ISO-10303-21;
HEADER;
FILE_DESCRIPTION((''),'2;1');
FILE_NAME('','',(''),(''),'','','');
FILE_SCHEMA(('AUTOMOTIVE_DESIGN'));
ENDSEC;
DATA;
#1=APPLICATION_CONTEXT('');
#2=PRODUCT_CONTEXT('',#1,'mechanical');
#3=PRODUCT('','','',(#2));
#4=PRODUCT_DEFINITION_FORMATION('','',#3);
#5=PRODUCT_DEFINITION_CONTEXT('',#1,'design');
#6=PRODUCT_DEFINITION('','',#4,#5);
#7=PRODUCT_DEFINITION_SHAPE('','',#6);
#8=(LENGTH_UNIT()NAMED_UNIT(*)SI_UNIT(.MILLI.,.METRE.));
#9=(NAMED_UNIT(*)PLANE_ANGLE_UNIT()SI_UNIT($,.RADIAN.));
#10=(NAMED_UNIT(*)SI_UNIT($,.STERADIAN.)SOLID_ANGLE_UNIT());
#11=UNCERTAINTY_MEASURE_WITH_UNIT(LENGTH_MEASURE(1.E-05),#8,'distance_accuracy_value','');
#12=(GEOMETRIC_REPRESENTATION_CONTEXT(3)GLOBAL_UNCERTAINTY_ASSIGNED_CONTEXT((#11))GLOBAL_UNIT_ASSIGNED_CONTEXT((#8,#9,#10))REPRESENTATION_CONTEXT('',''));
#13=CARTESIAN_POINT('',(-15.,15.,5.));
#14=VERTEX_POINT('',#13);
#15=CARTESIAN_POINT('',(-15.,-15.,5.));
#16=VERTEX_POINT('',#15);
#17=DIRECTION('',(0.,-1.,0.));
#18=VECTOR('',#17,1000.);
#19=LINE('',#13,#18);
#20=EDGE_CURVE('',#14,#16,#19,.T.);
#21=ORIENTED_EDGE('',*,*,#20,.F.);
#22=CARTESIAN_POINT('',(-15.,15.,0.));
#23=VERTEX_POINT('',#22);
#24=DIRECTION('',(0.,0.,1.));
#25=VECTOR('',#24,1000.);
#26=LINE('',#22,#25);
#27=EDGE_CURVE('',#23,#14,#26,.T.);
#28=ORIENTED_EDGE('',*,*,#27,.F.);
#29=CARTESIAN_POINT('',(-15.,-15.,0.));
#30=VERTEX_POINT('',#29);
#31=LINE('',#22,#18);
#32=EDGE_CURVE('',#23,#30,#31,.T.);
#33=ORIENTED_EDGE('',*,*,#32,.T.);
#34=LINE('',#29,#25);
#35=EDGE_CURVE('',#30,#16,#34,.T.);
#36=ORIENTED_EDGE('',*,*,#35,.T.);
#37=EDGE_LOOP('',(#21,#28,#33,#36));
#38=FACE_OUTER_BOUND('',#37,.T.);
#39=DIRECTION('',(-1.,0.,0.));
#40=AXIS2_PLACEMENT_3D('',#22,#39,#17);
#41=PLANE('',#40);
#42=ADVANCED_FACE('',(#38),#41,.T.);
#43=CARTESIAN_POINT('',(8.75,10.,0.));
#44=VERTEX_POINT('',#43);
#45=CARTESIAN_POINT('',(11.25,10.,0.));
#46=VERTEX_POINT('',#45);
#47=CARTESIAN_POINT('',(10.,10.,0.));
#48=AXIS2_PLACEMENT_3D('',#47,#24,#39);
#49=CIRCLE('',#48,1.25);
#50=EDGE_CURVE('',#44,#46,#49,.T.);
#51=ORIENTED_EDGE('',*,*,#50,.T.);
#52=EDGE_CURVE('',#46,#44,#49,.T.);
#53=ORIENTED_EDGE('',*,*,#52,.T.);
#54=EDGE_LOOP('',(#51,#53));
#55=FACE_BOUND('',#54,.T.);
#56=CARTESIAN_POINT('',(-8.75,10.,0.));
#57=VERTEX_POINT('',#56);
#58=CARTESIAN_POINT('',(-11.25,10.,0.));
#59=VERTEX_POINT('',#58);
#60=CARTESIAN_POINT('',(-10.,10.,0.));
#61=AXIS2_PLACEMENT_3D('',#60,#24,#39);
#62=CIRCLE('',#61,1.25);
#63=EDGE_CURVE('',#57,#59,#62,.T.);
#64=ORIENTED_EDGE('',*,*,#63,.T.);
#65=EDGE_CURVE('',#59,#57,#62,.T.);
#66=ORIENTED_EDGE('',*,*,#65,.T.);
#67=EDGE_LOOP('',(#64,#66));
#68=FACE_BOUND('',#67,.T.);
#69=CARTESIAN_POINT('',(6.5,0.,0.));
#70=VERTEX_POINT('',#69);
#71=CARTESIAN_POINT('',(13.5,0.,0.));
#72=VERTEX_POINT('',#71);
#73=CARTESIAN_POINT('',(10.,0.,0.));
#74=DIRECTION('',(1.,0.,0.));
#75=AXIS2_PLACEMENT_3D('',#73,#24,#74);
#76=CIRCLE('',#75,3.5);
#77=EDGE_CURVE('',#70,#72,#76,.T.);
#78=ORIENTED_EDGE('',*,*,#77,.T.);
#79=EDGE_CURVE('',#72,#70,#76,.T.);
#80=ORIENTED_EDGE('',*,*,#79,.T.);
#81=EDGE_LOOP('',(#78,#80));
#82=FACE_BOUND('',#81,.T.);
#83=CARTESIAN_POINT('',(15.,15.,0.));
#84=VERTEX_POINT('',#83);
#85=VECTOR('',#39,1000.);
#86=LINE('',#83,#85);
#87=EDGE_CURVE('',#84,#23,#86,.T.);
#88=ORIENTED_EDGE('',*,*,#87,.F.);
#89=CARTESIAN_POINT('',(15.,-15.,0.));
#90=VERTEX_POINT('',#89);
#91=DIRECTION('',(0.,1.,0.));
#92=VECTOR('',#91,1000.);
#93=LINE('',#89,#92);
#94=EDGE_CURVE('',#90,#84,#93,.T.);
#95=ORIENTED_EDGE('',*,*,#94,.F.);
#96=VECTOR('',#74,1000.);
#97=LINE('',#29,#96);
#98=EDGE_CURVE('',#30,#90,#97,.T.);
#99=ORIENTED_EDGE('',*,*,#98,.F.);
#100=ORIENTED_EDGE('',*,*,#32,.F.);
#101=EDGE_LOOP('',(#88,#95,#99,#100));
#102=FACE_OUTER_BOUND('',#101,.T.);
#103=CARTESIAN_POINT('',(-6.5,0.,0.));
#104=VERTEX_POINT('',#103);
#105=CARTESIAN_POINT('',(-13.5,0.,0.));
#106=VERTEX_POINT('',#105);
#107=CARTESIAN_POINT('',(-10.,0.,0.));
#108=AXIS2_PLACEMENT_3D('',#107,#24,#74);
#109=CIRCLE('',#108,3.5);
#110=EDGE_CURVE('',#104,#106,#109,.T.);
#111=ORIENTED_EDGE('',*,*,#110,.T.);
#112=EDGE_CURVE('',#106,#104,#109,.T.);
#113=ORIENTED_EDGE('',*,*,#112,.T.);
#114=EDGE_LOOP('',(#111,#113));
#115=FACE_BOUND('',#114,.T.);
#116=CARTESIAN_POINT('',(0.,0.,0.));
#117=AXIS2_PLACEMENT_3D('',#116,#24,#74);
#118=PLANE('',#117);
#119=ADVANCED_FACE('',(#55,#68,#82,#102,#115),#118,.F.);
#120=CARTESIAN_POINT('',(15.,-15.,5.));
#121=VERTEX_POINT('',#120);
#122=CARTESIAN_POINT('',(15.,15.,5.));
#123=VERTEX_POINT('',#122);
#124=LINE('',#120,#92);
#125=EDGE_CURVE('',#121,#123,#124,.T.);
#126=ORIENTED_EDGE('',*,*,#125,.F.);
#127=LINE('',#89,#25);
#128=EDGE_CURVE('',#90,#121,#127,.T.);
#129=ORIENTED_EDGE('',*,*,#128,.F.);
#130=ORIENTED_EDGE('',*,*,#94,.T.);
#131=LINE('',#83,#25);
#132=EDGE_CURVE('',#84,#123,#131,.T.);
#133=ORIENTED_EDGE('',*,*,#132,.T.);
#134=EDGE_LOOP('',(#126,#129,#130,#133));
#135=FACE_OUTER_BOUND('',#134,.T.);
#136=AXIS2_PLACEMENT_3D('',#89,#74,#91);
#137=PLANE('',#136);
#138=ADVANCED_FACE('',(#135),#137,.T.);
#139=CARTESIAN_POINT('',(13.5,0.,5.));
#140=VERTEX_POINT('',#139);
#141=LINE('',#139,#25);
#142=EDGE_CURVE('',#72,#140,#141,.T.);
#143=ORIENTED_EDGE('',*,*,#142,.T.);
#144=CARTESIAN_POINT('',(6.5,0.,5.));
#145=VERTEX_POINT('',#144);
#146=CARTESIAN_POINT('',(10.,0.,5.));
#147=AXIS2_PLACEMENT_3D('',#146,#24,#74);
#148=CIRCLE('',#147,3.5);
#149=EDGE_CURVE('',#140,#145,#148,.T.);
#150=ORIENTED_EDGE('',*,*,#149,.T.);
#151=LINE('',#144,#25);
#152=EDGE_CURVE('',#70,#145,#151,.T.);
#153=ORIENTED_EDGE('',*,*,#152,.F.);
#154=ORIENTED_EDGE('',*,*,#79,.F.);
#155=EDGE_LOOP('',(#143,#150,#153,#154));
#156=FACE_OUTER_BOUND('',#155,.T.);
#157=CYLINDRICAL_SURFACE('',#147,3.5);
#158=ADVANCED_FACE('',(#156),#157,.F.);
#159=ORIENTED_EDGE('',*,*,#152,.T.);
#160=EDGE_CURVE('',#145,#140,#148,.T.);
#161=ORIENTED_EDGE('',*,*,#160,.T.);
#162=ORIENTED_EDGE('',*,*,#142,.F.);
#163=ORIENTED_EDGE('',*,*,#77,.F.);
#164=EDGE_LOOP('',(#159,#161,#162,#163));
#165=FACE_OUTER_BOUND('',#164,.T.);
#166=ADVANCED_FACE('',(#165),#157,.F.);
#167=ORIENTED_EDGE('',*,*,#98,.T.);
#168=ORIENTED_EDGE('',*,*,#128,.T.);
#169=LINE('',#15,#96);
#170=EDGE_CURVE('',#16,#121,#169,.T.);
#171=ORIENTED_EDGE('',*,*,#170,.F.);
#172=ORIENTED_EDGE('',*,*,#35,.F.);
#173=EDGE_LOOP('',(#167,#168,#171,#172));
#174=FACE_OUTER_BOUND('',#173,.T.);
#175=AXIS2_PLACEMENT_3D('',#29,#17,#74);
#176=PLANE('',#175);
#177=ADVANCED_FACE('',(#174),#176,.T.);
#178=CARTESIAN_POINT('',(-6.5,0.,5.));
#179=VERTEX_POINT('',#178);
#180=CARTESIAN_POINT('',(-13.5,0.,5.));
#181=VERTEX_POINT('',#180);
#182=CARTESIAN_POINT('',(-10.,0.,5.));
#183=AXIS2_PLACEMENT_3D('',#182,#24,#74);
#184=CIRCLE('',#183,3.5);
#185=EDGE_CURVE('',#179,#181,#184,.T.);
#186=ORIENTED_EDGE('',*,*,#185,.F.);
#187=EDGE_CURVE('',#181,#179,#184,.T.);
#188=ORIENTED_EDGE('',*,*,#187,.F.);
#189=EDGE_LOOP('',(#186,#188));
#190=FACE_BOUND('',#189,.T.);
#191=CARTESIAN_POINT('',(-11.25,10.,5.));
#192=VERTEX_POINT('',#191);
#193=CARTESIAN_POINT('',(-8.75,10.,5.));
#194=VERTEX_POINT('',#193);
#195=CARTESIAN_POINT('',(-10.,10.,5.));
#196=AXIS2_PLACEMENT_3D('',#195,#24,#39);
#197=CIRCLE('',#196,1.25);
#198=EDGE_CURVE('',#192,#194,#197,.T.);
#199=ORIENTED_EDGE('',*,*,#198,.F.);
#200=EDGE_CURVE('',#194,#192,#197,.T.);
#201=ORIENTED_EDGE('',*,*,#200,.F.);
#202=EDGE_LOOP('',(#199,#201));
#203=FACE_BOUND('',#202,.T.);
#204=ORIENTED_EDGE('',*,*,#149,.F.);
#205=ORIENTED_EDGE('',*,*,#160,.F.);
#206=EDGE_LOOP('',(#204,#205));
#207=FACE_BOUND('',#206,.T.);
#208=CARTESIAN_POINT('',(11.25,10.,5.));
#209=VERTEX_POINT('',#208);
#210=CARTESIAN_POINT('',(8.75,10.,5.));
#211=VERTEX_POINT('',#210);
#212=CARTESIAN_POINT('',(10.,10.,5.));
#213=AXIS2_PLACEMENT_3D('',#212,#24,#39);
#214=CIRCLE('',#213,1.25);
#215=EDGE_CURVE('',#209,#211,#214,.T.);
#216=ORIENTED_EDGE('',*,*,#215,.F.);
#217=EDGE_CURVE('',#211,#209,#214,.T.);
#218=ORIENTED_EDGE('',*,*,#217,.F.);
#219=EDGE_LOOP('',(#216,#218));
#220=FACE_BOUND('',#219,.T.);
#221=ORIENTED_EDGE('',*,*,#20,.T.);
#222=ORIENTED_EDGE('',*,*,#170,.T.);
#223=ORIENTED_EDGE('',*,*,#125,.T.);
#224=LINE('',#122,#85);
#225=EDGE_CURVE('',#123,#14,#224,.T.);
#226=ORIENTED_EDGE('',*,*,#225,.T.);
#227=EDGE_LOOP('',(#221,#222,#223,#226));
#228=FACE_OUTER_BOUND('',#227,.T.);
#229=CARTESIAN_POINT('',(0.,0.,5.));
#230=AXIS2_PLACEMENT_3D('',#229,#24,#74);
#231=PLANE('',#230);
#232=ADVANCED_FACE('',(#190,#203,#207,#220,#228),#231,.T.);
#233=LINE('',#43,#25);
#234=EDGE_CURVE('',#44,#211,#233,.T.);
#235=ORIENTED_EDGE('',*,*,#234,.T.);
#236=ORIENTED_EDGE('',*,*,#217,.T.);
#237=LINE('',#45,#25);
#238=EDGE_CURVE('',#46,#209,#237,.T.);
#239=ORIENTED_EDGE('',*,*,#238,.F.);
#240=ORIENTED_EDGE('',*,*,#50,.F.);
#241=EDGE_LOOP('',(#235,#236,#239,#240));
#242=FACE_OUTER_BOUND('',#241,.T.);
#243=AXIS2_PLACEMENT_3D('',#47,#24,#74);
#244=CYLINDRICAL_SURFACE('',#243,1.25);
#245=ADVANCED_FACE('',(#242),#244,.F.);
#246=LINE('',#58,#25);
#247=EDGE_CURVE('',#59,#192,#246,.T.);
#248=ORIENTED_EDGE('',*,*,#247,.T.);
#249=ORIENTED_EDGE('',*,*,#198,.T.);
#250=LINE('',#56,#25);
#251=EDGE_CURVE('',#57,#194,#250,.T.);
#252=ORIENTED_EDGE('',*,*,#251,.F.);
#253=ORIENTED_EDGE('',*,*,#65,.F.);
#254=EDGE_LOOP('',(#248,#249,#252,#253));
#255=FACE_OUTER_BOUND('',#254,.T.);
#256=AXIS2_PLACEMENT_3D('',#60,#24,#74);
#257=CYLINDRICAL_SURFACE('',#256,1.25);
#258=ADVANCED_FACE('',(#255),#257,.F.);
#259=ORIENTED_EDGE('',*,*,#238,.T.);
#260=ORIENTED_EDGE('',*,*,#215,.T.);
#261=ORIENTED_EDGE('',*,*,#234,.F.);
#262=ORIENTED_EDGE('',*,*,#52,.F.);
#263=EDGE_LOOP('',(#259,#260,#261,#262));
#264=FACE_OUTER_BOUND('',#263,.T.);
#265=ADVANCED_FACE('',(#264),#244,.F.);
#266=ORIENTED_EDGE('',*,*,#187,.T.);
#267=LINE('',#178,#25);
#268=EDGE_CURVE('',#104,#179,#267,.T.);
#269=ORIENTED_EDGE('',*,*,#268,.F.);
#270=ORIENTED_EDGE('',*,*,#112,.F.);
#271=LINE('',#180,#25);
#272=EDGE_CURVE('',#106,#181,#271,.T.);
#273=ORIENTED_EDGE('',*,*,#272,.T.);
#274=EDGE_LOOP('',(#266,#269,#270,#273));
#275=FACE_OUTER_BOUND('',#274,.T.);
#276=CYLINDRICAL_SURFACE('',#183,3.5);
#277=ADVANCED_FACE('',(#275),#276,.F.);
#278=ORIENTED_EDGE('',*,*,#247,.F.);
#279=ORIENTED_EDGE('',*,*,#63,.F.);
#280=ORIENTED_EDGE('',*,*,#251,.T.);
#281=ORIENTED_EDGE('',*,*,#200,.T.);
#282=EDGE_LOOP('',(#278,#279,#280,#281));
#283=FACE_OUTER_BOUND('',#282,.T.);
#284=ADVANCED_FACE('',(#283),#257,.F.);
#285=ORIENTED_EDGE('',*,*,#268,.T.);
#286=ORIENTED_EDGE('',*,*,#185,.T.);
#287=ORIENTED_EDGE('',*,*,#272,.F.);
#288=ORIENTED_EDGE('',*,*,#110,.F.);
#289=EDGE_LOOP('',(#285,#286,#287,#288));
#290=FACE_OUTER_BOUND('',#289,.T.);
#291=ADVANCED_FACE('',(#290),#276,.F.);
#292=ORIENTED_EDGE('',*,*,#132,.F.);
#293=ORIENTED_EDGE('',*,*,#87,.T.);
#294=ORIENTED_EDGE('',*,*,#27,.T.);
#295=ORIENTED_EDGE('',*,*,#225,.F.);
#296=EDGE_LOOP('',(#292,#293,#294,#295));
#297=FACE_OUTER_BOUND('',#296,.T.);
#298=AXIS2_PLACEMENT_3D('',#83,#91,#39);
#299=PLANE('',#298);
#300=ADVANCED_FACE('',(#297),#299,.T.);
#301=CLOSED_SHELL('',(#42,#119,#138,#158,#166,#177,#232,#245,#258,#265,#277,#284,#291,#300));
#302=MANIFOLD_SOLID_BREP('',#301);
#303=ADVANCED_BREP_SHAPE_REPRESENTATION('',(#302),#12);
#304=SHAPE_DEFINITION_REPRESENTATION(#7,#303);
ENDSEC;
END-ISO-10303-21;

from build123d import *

# Parameters (mm, degrees)
SKETCH_1_W            = 30
SKETCH_1_H            = 30
SKETCH_1_R            = 1.25
EXTRUDE_1_DEPTH       = 5
HOLE_WIZARD_7_0_7_1_D = 7


with BuildPart() as part:
    # 草图1 → 凸台-拉伸1 (new body)
    with BuildSketch(Plane.XY.offset(5)):
        Rectangle(SKETCH_1_W, SKETCH_1_H)
        with Locations(Location((-10, 10, 0), (0, 0, 180))):
            Circle(SKETCH_1_R, mode=Mode.SUBTRACT)
        with Locations(Location((10, 10, 0), (0, 0, 180))):
            Circle(SKETCH_1_R, mode=Mode.SUBTRACT)
    extrude(amount=-EXTRUDE_1_DEPTH)

    # Ø7.0 (7) 直径孔1 (through all)
    with Locations(Plane.XY.offset(5)):
        with Locations((10, 0), (-10, 0)):
            Hole(HOLE_WIZARD_7_0_7_1_D / 2)


solid = part.part
